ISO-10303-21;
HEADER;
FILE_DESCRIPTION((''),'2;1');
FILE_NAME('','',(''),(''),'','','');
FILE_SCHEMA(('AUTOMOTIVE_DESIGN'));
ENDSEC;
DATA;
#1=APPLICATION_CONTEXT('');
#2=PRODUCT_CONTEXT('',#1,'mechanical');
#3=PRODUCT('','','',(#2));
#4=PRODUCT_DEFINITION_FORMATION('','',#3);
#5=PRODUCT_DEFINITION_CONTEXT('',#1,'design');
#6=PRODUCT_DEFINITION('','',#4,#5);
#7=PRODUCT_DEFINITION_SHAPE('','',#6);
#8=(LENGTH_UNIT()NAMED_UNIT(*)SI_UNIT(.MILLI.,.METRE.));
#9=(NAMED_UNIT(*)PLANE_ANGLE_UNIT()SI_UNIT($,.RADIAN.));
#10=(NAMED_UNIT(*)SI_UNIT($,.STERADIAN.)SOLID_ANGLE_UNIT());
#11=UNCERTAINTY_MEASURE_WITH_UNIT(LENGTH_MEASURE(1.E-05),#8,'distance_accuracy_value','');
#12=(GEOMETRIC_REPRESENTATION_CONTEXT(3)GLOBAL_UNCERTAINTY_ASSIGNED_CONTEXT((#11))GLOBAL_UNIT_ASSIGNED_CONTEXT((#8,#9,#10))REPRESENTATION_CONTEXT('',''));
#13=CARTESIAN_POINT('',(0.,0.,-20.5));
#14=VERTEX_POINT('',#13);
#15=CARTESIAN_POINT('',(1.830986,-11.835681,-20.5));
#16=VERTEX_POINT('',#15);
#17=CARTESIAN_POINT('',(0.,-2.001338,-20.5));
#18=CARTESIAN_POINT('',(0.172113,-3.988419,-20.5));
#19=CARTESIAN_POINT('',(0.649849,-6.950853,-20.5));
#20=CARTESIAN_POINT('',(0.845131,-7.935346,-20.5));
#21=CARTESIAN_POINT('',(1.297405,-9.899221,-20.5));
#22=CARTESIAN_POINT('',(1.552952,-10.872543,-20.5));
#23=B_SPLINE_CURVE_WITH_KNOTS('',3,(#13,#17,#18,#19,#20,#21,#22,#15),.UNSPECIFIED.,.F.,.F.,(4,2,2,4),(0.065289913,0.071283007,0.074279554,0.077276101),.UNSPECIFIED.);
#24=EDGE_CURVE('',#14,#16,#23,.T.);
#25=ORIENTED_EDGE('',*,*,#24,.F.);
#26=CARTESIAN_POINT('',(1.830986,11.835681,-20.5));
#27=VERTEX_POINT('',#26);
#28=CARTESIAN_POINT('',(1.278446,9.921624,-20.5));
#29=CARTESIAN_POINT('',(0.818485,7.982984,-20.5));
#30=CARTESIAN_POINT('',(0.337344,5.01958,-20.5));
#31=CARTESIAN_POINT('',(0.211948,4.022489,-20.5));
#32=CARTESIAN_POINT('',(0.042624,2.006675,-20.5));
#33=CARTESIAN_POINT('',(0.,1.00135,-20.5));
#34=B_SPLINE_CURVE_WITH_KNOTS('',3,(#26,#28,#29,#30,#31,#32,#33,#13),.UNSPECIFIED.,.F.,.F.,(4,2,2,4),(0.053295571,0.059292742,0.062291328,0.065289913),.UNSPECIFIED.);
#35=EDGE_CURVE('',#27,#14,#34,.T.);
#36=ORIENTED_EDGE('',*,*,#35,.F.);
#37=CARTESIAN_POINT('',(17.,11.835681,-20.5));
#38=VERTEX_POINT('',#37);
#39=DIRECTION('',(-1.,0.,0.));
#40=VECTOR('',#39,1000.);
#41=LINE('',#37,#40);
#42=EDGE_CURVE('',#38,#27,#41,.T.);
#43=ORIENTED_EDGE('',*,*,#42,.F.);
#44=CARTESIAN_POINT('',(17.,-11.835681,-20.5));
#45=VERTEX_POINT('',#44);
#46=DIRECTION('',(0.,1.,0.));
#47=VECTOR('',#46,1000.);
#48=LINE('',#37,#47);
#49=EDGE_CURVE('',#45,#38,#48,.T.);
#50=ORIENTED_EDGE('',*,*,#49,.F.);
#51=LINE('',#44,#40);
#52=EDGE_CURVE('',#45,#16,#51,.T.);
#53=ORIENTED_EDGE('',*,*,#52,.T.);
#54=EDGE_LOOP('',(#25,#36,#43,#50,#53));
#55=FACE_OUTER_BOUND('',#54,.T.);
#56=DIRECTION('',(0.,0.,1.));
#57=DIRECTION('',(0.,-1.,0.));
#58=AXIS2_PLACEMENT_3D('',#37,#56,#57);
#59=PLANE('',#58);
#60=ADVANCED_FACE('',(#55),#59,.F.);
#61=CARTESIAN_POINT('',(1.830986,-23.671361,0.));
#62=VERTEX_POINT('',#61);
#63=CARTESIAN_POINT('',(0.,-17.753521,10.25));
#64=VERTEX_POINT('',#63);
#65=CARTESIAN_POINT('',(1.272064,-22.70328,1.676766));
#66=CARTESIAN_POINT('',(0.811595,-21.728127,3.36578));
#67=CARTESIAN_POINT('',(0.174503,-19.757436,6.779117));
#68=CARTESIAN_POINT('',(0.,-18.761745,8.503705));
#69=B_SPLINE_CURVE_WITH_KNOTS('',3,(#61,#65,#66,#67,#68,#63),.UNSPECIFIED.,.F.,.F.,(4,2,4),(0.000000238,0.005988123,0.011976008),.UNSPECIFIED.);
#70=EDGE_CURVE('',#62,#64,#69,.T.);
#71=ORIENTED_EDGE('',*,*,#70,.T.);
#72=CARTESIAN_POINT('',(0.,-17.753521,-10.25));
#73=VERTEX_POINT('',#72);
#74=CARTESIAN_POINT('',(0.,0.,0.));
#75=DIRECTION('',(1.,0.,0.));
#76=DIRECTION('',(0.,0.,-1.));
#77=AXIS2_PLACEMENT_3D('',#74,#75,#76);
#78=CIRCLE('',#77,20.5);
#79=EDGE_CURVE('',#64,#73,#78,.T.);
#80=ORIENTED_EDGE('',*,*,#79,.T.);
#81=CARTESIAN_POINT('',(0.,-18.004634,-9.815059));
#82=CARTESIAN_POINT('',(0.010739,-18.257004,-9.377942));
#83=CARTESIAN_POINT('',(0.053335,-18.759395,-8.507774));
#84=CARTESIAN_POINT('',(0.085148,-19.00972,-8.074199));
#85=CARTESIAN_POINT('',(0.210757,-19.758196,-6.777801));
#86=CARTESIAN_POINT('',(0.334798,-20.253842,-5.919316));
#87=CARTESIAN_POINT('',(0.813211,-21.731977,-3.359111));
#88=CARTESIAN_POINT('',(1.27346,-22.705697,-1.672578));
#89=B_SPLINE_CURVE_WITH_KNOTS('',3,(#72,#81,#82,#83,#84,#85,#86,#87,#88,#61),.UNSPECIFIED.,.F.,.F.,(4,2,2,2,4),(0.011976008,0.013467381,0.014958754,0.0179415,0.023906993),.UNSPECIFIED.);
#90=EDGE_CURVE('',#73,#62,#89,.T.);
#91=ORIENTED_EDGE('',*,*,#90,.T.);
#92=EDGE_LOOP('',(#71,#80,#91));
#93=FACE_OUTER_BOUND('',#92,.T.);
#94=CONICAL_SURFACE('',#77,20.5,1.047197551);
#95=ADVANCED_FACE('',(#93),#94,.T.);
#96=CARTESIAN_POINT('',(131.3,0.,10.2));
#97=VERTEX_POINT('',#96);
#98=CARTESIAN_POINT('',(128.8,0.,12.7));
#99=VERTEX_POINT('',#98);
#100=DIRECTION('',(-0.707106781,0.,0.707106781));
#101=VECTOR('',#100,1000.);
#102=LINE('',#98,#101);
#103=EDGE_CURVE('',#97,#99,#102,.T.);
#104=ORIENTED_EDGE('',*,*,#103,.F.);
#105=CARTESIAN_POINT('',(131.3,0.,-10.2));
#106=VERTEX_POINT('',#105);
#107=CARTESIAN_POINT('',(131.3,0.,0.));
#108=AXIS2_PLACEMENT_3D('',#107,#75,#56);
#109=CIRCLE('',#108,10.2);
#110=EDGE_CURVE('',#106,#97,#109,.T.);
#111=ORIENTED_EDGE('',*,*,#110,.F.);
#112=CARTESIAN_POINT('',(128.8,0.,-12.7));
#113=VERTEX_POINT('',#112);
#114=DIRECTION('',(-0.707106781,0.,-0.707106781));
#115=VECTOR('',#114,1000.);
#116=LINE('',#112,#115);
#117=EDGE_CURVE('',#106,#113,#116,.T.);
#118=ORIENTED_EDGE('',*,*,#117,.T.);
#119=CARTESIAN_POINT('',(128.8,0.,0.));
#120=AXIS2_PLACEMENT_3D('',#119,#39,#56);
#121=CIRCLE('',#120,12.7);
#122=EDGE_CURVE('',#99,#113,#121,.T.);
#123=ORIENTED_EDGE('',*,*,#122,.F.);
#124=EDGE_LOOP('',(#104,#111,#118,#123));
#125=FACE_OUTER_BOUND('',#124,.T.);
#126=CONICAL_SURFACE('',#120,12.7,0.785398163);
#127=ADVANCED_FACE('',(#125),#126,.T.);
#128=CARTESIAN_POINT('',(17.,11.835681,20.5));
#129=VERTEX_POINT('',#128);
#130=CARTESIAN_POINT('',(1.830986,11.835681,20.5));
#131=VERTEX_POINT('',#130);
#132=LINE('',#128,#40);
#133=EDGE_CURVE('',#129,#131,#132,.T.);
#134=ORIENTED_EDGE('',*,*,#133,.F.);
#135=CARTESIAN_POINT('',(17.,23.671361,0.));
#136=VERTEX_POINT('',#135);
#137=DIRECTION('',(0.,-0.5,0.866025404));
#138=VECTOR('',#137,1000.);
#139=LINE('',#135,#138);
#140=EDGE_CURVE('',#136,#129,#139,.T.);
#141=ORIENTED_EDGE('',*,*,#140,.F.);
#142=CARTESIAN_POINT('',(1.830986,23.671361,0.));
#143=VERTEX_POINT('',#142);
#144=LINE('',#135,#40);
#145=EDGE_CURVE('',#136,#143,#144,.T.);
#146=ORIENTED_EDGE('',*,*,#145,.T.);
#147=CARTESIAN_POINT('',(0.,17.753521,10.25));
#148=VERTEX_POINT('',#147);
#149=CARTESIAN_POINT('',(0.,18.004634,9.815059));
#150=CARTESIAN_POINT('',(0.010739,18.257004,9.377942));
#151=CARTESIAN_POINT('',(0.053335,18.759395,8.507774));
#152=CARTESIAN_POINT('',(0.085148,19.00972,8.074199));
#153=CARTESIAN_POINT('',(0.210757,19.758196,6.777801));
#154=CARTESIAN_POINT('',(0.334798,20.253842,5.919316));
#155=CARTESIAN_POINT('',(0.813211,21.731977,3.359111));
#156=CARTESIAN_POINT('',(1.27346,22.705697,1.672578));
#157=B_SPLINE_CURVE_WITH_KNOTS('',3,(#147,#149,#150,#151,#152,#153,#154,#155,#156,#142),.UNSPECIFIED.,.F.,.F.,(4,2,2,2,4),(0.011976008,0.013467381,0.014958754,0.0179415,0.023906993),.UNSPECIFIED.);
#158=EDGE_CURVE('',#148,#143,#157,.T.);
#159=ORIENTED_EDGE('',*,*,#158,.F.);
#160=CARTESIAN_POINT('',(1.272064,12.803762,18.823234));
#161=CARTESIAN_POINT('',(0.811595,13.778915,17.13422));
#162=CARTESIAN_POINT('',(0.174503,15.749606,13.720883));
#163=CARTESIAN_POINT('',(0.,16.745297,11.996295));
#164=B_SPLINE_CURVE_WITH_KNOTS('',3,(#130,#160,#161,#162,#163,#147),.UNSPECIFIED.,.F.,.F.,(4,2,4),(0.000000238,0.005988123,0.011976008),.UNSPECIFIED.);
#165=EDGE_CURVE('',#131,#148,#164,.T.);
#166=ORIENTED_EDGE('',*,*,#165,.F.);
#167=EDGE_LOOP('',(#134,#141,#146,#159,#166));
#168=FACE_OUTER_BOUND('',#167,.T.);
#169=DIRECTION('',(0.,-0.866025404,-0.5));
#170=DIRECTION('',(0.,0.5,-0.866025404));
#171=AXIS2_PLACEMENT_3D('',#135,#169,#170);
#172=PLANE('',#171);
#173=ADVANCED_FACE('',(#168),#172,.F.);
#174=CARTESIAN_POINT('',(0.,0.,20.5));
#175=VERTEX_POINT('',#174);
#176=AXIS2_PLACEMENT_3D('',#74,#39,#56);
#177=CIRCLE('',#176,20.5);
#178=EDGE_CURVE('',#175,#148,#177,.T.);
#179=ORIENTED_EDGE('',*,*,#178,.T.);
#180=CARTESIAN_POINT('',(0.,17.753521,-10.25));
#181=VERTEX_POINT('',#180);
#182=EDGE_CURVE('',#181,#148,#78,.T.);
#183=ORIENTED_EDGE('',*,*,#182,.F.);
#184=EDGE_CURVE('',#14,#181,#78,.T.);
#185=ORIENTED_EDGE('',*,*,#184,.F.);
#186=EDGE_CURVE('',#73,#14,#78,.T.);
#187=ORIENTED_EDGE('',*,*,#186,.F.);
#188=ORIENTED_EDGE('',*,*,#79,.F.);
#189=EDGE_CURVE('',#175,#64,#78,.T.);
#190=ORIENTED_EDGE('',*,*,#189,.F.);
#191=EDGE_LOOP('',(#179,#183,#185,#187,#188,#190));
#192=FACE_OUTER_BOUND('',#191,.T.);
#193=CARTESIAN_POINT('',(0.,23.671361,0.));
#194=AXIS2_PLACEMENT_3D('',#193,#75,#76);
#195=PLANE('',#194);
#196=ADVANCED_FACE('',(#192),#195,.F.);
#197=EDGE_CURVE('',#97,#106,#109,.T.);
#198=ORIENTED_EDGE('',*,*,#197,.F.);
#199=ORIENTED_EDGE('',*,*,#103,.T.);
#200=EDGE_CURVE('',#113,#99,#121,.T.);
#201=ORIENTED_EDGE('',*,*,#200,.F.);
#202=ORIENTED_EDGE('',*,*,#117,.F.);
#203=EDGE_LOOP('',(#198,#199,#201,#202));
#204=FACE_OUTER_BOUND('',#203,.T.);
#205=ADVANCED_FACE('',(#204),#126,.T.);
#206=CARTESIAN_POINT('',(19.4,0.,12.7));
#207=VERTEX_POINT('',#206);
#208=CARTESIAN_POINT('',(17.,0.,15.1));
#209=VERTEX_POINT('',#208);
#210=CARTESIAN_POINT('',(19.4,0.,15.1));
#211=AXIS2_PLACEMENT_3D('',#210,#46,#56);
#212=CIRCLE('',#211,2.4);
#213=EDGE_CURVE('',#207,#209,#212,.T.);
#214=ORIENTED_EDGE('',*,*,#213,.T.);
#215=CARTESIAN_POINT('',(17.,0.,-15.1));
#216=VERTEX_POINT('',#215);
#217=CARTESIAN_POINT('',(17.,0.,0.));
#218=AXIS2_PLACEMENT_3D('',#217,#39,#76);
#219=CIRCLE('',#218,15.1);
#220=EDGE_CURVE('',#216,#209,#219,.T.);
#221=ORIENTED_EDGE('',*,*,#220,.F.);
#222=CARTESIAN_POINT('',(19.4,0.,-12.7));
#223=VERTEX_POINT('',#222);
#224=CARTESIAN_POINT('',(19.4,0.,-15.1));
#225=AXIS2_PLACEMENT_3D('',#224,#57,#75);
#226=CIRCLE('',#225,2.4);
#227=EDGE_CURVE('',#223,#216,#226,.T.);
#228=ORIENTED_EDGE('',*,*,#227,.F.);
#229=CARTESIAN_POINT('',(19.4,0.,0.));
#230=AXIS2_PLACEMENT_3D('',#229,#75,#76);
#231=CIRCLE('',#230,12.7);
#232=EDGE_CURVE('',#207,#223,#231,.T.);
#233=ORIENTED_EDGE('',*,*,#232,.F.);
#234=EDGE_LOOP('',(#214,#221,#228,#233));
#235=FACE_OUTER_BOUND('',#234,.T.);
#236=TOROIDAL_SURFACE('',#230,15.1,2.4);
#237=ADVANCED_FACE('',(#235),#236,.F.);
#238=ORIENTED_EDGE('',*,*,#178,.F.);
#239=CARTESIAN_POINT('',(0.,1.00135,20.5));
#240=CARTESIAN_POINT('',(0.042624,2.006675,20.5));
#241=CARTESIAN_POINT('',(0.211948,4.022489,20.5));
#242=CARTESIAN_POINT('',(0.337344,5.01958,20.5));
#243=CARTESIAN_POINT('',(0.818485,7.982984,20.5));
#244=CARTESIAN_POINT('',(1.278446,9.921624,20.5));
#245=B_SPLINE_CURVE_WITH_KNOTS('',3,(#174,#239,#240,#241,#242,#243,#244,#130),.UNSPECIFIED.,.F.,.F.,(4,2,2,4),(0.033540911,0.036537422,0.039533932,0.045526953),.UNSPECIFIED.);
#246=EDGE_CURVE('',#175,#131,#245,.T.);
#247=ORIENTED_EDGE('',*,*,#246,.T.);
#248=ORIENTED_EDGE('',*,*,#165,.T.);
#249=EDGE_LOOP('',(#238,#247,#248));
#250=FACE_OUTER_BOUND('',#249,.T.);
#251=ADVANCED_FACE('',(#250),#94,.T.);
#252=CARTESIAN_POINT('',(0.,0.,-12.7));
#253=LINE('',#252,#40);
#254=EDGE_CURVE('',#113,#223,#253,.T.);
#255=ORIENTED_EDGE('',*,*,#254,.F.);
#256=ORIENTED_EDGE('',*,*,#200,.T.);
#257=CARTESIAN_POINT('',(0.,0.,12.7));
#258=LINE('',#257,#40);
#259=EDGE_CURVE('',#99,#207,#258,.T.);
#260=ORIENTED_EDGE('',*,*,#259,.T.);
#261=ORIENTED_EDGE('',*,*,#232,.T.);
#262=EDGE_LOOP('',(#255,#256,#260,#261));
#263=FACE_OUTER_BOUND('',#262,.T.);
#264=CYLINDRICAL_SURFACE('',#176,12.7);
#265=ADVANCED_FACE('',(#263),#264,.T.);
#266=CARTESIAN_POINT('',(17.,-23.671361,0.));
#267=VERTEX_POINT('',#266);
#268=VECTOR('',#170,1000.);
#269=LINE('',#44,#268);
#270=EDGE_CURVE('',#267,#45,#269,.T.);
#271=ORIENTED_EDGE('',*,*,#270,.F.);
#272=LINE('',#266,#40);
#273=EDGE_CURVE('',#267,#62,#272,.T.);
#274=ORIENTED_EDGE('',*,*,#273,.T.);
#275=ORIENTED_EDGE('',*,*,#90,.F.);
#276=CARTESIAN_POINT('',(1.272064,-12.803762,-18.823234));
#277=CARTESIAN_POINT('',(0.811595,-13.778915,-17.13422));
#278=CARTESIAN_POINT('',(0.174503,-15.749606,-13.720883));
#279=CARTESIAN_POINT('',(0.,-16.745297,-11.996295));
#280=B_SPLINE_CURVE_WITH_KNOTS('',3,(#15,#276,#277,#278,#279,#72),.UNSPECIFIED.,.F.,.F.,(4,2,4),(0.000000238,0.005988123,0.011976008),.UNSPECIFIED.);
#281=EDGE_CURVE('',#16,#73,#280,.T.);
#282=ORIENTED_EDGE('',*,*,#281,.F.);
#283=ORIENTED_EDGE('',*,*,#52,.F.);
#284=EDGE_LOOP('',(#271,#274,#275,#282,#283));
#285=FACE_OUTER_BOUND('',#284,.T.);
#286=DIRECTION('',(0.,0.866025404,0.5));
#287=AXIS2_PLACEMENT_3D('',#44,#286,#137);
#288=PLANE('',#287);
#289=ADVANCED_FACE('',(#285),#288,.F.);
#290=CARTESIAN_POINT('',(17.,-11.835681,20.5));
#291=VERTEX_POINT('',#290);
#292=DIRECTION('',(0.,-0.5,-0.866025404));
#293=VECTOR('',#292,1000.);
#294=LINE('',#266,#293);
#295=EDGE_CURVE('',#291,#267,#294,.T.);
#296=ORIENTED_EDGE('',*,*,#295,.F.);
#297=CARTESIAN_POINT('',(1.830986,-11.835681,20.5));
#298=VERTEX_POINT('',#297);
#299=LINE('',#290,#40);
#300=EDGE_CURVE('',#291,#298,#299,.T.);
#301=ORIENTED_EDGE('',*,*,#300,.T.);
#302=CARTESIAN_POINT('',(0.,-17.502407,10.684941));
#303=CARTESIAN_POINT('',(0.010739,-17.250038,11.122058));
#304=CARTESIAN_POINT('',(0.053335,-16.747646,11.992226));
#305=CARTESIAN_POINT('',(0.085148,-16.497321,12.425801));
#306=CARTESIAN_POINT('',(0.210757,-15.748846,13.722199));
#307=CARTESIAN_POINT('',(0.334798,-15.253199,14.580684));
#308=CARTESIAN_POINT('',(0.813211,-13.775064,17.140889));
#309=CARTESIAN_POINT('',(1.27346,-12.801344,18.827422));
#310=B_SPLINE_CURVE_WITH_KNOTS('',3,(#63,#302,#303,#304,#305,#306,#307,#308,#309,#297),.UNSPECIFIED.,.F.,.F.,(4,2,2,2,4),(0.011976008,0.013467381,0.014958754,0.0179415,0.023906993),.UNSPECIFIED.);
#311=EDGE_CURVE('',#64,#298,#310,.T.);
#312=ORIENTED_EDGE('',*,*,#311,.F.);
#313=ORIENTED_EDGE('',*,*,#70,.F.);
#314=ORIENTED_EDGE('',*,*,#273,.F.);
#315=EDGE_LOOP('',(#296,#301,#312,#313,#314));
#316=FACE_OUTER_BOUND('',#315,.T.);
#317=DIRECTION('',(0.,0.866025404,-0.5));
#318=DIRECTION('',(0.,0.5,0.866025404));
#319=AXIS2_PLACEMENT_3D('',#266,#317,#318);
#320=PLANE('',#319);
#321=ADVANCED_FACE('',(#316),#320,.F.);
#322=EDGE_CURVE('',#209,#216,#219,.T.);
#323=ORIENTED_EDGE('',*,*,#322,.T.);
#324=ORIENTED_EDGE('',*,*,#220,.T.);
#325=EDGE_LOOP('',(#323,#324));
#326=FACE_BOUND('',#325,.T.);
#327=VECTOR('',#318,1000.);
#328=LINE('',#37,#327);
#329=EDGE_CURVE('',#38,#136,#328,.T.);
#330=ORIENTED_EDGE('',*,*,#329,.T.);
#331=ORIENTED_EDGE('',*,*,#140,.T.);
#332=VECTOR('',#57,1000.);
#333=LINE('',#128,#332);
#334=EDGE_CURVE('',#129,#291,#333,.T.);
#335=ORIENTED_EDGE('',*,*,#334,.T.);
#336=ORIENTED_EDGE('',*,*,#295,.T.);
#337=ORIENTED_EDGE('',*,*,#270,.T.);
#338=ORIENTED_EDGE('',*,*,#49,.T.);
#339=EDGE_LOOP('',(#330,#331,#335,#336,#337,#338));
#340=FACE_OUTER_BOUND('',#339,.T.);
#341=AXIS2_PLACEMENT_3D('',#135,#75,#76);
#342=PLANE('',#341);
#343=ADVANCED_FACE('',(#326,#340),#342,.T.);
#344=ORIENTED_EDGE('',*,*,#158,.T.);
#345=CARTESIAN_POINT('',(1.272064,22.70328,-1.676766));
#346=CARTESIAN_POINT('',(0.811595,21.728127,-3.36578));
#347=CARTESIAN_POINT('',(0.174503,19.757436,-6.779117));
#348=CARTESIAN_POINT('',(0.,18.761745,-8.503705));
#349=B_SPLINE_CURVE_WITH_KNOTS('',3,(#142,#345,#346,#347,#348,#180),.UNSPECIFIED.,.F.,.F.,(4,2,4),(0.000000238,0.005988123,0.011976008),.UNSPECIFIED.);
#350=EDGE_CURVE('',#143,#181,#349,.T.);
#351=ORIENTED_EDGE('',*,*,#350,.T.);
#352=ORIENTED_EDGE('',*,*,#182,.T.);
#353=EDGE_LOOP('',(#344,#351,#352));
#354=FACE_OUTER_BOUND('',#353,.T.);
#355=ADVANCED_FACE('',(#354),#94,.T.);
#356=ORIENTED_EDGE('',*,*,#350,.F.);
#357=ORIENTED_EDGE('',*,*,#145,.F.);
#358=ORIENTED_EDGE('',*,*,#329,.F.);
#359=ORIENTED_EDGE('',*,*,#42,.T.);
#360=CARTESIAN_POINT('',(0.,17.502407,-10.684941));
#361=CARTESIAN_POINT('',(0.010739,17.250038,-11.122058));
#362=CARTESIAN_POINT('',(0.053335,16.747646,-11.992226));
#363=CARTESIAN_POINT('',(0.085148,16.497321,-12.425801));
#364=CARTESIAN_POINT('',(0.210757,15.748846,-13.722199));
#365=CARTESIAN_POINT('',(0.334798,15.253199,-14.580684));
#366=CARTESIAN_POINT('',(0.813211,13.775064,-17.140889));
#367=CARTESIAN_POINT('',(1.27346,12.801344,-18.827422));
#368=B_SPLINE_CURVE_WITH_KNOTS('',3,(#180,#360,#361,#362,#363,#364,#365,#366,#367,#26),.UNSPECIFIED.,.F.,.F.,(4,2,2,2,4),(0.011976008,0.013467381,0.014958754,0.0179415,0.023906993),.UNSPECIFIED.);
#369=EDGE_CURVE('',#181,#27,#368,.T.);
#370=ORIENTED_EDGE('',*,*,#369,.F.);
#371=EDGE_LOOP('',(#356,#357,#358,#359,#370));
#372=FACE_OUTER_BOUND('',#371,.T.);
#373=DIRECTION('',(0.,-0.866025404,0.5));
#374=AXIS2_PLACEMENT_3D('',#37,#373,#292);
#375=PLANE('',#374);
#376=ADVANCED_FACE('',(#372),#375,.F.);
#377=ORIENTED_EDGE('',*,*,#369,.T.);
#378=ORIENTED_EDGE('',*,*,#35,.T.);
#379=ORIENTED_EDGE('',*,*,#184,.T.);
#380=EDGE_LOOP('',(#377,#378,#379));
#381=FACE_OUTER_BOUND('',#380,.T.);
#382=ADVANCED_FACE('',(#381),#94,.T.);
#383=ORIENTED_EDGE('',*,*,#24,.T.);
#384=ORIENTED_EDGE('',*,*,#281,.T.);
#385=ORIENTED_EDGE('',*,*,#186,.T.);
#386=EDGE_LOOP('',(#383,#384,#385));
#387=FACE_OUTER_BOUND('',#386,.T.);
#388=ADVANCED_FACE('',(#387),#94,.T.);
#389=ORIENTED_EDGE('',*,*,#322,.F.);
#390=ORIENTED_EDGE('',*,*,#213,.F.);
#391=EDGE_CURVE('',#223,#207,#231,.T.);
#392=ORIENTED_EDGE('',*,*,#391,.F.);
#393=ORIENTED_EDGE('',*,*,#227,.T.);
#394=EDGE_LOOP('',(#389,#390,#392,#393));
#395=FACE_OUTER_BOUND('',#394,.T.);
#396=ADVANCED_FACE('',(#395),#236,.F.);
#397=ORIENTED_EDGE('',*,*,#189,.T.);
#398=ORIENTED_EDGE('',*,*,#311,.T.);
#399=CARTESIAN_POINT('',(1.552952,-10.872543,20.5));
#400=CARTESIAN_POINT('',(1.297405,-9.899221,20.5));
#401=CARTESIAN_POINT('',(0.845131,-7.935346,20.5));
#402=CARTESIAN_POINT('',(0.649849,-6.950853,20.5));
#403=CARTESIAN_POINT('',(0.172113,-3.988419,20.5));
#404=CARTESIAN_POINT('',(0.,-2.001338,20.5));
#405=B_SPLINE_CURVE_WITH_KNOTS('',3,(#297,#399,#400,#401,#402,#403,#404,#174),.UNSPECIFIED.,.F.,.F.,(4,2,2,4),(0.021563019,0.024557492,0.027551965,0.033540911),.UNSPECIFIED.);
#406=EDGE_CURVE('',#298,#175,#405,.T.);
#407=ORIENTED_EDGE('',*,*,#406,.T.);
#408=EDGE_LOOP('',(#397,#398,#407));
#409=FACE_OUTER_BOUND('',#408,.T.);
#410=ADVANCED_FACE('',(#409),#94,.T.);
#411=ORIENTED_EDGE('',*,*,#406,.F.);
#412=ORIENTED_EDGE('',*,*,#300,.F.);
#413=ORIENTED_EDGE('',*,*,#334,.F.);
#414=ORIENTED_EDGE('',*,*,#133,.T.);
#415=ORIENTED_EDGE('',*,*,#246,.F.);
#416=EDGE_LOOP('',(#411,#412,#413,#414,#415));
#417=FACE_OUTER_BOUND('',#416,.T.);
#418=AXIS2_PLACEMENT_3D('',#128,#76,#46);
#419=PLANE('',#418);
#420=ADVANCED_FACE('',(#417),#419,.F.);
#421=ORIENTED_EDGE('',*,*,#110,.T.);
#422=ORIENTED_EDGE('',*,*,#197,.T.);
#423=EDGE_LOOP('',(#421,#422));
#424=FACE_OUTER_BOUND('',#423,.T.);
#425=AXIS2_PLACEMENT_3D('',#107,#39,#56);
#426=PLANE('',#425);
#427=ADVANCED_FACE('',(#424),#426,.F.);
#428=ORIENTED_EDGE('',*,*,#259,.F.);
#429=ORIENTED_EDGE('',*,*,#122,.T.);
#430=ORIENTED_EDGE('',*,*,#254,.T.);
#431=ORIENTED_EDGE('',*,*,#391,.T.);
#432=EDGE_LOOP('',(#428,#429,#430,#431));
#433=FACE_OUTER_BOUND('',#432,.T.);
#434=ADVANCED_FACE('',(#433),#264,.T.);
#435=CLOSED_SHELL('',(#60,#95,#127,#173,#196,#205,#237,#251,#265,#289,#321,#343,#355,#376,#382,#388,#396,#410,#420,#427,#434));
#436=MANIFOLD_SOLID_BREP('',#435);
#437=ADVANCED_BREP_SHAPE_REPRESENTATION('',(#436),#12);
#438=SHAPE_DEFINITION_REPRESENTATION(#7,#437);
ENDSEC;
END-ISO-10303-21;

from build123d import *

# Parameters (mm, degrees)
BASE_EXTRUDE_DEPTH = 17
CHAMFER_2_SIZE     = 2.5
FILLET_2_R         = 2.4


with BuildPart() as part:
    # Sketch1 → Base-Extrude (new body)
    with BuildSketch(Plane(origin=(0, 0, 0), x_dir=(0, 0, -1), z_dir=(1, 0, 0))):
        Polygon((20.5, 11.835680518), (20.5, -11.835680518), (0, -23.671361037), (-20.5, -11.835680518), (-20.5, 11.835680518), (0, 23.671361037), align=None)
    extrude(amount=BASE_EXTRUDE_DEPTH)

    # Sketch2 → Boss-Revolve1 (revolve)
    with BuildSketch(Plane.XY, mode=Mode.PRIVATE) as boss_revolve1_sk:
        Polygon((0, 0), (131.3, 0), (131.3, 10.902), (131.3, 12.7), (27.8072, 12.7), (0, 12.7), align=None)
    revolve(boss_revolve1_sk.sketch.rotate(Axis((0, 0, 0), (1, 0, 0)), 90), axis=Axis((0, 0, 0), (1, 0, 0)))

    # Sketch3 → Cut-Revolve1 (revolve, cut)
    with BuildSketch(Plane.XY):
        Polygon((0, 20.5), (4.717737494, 28.671361037), (4.717737494, 33.671361037), (-10, 33.671361037), (-10, 20.5), align=None)
    revolve(axis=Axis((0, 0, 0), (1, 0, 0)), mode=Mode.SUBTRACT)

    # Chamfer 2
    chamfer_2_edges = [part.edges().sort_by_distance(p)[0] for p in [
        (131.3, 0, -12.7),
    ]]
    chamfer(chamfer_2_edges, length=CHAMFER_2_SIZE)

    # Fillet 2
    fillet_2_edges = [part.edges().sort_by_distance(p)[0] for p in [
        (17, 0, -12.7),
    ]]
    fillet(fillet_2_edges, radius=FILLET_2_R)


solid = part.part
